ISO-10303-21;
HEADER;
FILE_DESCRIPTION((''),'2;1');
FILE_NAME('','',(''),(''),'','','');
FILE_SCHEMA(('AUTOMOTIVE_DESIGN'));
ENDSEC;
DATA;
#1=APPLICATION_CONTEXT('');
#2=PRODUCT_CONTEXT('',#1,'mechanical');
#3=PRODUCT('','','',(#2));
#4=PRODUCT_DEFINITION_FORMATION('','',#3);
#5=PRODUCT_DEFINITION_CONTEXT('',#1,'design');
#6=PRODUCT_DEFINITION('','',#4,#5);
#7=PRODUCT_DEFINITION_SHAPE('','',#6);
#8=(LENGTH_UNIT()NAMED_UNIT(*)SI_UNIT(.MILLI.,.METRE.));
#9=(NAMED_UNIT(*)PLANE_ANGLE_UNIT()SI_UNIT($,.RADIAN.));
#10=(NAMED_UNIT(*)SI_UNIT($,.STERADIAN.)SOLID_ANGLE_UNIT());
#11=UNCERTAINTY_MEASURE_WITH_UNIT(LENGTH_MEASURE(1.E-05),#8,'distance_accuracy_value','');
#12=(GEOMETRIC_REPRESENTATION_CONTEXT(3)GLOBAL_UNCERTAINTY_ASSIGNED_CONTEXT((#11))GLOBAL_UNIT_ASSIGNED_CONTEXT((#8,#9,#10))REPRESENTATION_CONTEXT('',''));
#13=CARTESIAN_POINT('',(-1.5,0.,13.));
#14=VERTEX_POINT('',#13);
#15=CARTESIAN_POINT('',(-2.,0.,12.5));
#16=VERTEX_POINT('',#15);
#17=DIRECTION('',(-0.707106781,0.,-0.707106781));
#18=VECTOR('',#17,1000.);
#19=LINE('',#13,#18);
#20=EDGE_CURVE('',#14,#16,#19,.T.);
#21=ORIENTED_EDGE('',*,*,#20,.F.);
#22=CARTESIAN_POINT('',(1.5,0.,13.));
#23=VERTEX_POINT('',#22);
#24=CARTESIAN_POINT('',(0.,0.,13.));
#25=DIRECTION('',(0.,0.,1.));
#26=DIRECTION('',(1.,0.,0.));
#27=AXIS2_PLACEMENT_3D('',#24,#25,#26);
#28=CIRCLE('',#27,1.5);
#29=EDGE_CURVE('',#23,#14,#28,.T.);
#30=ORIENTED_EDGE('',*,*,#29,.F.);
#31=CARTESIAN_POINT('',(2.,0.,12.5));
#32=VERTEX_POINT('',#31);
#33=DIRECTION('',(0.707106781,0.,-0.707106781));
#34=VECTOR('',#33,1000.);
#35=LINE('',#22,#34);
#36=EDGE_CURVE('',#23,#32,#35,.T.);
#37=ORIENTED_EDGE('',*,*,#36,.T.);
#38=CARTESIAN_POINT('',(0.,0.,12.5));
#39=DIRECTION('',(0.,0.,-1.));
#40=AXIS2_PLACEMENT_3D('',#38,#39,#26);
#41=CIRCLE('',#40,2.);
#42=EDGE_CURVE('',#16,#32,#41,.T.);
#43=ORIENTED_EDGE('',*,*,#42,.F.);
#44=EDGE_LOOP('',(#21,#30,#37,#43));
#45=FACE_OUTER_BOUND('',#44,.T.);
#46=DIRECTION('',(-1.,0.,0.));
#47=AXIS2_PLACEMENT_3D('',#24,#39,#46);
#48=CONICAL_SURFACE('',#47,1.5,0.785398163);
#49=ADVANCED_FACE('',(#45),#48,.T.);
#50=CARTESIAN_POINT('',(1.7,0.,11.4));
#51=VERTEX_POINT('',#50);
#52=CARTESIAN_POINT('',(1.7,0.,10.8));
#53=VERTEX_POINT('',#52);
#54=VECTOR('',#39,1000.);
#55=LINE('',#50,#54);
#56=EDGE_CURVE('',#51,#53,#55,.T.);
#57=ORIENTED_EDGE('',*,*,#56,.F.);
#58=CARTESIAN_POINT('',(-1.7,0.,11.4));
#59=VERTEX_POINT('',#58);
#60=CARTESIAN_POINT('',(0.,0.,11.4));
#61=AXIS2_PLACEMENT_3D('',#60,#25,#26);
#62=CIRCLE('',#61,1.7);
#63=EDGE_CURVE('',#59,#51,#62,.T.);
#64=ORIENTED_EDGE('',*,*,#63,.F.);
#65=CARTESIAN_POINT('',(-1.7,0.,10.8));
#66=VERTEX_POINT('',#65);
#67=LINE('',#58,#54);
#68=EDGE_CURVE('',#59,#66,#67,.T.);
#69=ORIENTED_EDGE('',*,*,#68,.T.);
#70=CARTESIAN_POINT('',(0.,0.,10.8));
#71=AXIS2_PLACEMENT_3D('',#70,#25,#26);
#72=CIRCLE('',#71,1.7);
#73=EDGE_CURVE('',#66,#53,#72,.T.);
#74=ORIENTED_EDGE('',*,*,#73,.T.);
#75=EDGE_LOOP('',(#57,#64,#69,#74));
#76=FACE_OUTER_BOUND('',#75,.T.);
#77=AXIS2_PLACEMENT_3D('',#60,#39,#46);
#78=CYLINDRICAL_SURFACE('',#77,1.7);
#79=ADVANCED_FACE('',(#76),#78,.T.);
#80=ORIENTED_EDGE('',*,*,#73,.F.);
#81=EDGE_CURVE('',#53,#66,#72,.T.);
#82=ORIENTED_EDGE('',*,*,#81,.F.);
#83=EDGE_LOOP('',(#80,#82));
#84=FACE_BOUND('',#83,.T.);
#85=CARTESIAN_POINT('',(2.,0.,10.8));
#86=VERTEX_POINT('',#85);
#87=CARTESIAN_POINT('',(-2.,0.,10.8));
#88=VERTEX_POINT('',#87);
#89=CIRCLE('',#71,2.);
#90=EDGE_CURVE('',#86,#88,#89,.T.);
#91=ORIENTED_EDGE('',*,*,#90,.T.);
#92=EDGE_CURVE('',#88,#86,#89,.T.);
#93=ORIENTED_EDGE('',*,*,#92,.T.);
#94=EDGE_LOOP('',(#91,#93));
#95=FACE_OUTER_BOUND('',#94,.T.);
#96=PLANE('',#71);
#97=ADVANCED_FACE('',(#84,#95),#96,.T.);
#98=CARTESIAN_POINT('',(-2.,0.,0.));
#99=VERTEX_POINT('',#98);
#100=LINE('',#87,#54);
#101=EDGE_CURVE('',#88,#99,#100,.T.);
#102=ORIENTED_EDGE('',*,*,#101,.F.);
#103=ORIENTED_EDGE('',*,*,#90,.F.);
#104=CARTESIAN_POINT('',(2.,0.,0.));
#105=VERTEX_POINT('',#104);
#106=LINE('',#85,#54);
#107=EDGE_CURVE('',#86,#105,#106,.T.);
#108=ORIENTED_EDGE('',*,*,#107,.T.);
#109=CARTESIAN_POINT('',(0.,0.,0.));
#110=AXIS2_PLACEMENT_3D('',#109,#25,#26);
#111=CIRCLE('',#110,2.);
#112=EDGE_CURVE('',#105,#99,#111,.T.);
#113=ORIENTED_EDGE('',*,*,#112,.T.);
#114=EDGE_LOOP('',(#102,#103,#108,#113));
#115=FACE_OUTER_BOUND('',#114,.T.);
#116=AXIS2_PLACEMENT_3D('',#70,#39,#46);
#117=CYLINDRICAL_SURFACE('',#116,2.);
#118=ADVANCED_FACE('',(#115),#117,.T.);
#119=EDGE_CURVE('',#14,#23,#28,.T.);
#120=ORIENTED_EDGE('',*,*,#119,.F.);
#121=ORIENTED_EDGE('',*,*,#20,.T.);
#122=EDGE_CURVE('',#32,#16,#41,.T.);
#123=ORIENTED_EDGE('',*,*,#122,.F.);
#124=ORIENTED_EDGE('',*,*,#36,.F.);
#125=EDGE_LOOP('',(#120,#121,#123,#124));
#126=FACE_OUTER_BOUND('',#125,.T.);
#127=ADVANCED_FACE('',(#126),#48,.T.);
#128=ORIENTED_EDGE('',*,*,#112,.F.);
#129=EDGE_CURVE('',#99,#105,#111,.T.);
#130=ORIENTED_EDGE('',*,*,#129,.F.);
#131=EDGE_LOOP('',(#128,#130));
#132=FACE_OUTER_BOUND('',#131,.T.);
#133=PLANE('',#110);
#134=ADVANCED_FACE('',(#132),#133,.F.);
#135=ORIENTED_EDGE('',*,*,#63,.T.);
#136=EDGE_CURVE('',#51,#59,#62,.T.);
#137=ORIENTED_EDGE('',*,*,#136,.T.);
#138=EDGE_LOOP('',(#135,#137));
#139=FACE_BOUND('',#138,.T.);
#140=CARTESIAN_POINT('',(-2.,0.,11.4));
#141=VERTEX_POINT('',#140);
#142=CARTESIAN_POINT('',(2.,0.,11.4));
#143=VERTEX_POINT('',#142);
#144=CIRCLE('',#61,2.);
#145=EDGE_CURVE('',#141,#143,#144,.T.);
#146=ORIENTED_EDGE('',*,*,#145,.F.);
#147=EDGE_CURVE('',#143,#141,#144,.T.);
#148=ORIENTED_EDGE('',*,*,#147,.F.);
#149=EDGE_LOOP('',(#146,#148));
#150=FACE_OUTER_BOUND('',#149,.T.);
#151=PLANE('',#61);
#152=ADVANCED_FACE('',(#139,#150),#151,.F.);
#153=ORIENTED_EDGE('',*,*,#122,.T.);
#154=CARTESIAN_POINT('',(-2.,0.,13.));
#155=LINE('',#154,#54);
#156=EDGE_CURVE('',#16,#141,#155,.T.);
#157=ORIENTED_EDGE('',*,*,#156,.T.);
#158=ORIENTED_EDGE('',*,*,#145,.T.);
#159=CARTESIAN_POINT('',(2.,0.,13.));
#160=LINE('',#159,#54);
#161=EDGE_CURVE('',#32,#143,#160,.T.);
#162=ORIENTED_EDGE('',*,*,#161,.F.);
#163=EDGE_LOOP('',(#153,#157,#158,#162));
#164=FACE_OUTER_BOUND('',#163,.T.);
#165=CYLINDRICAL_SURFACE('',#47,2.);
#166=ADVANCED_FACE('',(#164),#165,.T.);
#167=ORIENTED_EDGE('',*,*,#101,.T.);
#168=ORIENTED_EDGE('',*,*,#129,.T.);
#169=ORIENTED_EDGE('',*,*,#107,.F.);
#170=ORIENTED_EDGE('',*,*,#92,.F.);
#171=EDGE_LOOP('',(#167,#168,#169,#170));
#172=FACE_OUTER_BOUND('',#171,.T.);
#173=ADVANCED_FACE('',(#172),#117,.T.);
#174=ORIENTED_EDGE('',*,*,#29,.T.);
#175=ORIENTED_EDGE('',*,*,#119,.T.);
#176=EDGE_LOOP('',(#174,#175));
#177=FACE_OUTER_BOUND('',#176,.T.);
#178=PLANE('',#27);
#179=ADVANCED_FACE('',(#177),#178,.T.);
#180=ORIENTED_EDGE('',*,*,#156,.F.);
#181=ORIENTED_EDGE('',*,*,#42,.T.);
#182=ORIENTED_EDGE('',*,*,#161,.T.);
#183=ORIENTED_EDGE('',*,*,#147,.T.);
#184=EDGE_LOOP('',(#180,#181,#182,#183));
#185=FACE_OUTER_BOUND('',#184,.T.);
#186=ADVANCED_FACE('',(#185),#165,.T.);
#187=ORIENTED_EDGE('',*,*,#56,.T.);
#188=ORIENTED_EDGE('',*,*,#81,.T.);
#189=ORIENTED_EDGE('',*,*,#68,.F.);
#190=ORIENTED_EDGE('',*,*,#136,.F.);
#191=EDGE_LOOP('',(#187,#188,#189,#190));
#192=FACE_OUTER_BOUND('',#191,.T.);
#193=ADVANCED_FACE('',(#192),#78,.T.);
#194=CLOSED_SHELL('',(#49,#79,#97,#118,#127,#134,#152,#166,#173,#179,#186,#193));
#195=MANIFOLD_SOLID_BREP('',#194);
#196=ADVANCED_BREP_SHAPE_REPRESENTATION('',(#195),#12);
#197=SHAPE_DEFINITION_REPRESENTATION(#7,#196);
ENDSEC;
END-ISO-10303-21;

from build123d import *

# Parameters (mm, degrees)
SKETCH1_R           = 2
BOSS_EXTRUDE1_DEPTH = 10.8
SKETCH2_R           = 1.7
BOSS_EXTRUDE2_DEPTH = 0.6
SKETCH3_R           = 2
BOSS_EXTRUDE3_DEPTH = 1.6
CHAMFER1_SIZE       = 0.5


with BuildPart() as part:
    # Sketch1 → Boss-Extrude1 (new body)
    with BuildSketch(Plane.XY):
        with Locations(Location((0, 0, 0), (0, 0, 180))):
            Circle(SKETCH1_R)
    extrude(amount=BOSS_EXTRUDE1_DEPTH)

    # Sketch2 → Boss-Extrude2 (add)
    with BuildSketch(Plane.XY.offset(10.8)):
        Circle(SKETCH2_R)
    extrude(amount=BOSS_EXTRUDE2_DEPTH)

    # Sketch3 → Boss-Extrude3 (add)
    with BuildSketch(Plane.XY.offset(11.4)):
        with Locations(Location((0, 0, 0), (0, 0, 180))):
            Circle(SKETCH3_R)
    extrude(amount=BOSS_EXTRUDE3_DEPTH)

    # Chamfer1
    chamfer1_edges = [part.edges().sort_by_distance(p)[0] for p in [
        (2, 0, 13),
    ]]
    chamfer(chamfer1_edges, length=CHAMFER1_SIZE)


solid = part.part
